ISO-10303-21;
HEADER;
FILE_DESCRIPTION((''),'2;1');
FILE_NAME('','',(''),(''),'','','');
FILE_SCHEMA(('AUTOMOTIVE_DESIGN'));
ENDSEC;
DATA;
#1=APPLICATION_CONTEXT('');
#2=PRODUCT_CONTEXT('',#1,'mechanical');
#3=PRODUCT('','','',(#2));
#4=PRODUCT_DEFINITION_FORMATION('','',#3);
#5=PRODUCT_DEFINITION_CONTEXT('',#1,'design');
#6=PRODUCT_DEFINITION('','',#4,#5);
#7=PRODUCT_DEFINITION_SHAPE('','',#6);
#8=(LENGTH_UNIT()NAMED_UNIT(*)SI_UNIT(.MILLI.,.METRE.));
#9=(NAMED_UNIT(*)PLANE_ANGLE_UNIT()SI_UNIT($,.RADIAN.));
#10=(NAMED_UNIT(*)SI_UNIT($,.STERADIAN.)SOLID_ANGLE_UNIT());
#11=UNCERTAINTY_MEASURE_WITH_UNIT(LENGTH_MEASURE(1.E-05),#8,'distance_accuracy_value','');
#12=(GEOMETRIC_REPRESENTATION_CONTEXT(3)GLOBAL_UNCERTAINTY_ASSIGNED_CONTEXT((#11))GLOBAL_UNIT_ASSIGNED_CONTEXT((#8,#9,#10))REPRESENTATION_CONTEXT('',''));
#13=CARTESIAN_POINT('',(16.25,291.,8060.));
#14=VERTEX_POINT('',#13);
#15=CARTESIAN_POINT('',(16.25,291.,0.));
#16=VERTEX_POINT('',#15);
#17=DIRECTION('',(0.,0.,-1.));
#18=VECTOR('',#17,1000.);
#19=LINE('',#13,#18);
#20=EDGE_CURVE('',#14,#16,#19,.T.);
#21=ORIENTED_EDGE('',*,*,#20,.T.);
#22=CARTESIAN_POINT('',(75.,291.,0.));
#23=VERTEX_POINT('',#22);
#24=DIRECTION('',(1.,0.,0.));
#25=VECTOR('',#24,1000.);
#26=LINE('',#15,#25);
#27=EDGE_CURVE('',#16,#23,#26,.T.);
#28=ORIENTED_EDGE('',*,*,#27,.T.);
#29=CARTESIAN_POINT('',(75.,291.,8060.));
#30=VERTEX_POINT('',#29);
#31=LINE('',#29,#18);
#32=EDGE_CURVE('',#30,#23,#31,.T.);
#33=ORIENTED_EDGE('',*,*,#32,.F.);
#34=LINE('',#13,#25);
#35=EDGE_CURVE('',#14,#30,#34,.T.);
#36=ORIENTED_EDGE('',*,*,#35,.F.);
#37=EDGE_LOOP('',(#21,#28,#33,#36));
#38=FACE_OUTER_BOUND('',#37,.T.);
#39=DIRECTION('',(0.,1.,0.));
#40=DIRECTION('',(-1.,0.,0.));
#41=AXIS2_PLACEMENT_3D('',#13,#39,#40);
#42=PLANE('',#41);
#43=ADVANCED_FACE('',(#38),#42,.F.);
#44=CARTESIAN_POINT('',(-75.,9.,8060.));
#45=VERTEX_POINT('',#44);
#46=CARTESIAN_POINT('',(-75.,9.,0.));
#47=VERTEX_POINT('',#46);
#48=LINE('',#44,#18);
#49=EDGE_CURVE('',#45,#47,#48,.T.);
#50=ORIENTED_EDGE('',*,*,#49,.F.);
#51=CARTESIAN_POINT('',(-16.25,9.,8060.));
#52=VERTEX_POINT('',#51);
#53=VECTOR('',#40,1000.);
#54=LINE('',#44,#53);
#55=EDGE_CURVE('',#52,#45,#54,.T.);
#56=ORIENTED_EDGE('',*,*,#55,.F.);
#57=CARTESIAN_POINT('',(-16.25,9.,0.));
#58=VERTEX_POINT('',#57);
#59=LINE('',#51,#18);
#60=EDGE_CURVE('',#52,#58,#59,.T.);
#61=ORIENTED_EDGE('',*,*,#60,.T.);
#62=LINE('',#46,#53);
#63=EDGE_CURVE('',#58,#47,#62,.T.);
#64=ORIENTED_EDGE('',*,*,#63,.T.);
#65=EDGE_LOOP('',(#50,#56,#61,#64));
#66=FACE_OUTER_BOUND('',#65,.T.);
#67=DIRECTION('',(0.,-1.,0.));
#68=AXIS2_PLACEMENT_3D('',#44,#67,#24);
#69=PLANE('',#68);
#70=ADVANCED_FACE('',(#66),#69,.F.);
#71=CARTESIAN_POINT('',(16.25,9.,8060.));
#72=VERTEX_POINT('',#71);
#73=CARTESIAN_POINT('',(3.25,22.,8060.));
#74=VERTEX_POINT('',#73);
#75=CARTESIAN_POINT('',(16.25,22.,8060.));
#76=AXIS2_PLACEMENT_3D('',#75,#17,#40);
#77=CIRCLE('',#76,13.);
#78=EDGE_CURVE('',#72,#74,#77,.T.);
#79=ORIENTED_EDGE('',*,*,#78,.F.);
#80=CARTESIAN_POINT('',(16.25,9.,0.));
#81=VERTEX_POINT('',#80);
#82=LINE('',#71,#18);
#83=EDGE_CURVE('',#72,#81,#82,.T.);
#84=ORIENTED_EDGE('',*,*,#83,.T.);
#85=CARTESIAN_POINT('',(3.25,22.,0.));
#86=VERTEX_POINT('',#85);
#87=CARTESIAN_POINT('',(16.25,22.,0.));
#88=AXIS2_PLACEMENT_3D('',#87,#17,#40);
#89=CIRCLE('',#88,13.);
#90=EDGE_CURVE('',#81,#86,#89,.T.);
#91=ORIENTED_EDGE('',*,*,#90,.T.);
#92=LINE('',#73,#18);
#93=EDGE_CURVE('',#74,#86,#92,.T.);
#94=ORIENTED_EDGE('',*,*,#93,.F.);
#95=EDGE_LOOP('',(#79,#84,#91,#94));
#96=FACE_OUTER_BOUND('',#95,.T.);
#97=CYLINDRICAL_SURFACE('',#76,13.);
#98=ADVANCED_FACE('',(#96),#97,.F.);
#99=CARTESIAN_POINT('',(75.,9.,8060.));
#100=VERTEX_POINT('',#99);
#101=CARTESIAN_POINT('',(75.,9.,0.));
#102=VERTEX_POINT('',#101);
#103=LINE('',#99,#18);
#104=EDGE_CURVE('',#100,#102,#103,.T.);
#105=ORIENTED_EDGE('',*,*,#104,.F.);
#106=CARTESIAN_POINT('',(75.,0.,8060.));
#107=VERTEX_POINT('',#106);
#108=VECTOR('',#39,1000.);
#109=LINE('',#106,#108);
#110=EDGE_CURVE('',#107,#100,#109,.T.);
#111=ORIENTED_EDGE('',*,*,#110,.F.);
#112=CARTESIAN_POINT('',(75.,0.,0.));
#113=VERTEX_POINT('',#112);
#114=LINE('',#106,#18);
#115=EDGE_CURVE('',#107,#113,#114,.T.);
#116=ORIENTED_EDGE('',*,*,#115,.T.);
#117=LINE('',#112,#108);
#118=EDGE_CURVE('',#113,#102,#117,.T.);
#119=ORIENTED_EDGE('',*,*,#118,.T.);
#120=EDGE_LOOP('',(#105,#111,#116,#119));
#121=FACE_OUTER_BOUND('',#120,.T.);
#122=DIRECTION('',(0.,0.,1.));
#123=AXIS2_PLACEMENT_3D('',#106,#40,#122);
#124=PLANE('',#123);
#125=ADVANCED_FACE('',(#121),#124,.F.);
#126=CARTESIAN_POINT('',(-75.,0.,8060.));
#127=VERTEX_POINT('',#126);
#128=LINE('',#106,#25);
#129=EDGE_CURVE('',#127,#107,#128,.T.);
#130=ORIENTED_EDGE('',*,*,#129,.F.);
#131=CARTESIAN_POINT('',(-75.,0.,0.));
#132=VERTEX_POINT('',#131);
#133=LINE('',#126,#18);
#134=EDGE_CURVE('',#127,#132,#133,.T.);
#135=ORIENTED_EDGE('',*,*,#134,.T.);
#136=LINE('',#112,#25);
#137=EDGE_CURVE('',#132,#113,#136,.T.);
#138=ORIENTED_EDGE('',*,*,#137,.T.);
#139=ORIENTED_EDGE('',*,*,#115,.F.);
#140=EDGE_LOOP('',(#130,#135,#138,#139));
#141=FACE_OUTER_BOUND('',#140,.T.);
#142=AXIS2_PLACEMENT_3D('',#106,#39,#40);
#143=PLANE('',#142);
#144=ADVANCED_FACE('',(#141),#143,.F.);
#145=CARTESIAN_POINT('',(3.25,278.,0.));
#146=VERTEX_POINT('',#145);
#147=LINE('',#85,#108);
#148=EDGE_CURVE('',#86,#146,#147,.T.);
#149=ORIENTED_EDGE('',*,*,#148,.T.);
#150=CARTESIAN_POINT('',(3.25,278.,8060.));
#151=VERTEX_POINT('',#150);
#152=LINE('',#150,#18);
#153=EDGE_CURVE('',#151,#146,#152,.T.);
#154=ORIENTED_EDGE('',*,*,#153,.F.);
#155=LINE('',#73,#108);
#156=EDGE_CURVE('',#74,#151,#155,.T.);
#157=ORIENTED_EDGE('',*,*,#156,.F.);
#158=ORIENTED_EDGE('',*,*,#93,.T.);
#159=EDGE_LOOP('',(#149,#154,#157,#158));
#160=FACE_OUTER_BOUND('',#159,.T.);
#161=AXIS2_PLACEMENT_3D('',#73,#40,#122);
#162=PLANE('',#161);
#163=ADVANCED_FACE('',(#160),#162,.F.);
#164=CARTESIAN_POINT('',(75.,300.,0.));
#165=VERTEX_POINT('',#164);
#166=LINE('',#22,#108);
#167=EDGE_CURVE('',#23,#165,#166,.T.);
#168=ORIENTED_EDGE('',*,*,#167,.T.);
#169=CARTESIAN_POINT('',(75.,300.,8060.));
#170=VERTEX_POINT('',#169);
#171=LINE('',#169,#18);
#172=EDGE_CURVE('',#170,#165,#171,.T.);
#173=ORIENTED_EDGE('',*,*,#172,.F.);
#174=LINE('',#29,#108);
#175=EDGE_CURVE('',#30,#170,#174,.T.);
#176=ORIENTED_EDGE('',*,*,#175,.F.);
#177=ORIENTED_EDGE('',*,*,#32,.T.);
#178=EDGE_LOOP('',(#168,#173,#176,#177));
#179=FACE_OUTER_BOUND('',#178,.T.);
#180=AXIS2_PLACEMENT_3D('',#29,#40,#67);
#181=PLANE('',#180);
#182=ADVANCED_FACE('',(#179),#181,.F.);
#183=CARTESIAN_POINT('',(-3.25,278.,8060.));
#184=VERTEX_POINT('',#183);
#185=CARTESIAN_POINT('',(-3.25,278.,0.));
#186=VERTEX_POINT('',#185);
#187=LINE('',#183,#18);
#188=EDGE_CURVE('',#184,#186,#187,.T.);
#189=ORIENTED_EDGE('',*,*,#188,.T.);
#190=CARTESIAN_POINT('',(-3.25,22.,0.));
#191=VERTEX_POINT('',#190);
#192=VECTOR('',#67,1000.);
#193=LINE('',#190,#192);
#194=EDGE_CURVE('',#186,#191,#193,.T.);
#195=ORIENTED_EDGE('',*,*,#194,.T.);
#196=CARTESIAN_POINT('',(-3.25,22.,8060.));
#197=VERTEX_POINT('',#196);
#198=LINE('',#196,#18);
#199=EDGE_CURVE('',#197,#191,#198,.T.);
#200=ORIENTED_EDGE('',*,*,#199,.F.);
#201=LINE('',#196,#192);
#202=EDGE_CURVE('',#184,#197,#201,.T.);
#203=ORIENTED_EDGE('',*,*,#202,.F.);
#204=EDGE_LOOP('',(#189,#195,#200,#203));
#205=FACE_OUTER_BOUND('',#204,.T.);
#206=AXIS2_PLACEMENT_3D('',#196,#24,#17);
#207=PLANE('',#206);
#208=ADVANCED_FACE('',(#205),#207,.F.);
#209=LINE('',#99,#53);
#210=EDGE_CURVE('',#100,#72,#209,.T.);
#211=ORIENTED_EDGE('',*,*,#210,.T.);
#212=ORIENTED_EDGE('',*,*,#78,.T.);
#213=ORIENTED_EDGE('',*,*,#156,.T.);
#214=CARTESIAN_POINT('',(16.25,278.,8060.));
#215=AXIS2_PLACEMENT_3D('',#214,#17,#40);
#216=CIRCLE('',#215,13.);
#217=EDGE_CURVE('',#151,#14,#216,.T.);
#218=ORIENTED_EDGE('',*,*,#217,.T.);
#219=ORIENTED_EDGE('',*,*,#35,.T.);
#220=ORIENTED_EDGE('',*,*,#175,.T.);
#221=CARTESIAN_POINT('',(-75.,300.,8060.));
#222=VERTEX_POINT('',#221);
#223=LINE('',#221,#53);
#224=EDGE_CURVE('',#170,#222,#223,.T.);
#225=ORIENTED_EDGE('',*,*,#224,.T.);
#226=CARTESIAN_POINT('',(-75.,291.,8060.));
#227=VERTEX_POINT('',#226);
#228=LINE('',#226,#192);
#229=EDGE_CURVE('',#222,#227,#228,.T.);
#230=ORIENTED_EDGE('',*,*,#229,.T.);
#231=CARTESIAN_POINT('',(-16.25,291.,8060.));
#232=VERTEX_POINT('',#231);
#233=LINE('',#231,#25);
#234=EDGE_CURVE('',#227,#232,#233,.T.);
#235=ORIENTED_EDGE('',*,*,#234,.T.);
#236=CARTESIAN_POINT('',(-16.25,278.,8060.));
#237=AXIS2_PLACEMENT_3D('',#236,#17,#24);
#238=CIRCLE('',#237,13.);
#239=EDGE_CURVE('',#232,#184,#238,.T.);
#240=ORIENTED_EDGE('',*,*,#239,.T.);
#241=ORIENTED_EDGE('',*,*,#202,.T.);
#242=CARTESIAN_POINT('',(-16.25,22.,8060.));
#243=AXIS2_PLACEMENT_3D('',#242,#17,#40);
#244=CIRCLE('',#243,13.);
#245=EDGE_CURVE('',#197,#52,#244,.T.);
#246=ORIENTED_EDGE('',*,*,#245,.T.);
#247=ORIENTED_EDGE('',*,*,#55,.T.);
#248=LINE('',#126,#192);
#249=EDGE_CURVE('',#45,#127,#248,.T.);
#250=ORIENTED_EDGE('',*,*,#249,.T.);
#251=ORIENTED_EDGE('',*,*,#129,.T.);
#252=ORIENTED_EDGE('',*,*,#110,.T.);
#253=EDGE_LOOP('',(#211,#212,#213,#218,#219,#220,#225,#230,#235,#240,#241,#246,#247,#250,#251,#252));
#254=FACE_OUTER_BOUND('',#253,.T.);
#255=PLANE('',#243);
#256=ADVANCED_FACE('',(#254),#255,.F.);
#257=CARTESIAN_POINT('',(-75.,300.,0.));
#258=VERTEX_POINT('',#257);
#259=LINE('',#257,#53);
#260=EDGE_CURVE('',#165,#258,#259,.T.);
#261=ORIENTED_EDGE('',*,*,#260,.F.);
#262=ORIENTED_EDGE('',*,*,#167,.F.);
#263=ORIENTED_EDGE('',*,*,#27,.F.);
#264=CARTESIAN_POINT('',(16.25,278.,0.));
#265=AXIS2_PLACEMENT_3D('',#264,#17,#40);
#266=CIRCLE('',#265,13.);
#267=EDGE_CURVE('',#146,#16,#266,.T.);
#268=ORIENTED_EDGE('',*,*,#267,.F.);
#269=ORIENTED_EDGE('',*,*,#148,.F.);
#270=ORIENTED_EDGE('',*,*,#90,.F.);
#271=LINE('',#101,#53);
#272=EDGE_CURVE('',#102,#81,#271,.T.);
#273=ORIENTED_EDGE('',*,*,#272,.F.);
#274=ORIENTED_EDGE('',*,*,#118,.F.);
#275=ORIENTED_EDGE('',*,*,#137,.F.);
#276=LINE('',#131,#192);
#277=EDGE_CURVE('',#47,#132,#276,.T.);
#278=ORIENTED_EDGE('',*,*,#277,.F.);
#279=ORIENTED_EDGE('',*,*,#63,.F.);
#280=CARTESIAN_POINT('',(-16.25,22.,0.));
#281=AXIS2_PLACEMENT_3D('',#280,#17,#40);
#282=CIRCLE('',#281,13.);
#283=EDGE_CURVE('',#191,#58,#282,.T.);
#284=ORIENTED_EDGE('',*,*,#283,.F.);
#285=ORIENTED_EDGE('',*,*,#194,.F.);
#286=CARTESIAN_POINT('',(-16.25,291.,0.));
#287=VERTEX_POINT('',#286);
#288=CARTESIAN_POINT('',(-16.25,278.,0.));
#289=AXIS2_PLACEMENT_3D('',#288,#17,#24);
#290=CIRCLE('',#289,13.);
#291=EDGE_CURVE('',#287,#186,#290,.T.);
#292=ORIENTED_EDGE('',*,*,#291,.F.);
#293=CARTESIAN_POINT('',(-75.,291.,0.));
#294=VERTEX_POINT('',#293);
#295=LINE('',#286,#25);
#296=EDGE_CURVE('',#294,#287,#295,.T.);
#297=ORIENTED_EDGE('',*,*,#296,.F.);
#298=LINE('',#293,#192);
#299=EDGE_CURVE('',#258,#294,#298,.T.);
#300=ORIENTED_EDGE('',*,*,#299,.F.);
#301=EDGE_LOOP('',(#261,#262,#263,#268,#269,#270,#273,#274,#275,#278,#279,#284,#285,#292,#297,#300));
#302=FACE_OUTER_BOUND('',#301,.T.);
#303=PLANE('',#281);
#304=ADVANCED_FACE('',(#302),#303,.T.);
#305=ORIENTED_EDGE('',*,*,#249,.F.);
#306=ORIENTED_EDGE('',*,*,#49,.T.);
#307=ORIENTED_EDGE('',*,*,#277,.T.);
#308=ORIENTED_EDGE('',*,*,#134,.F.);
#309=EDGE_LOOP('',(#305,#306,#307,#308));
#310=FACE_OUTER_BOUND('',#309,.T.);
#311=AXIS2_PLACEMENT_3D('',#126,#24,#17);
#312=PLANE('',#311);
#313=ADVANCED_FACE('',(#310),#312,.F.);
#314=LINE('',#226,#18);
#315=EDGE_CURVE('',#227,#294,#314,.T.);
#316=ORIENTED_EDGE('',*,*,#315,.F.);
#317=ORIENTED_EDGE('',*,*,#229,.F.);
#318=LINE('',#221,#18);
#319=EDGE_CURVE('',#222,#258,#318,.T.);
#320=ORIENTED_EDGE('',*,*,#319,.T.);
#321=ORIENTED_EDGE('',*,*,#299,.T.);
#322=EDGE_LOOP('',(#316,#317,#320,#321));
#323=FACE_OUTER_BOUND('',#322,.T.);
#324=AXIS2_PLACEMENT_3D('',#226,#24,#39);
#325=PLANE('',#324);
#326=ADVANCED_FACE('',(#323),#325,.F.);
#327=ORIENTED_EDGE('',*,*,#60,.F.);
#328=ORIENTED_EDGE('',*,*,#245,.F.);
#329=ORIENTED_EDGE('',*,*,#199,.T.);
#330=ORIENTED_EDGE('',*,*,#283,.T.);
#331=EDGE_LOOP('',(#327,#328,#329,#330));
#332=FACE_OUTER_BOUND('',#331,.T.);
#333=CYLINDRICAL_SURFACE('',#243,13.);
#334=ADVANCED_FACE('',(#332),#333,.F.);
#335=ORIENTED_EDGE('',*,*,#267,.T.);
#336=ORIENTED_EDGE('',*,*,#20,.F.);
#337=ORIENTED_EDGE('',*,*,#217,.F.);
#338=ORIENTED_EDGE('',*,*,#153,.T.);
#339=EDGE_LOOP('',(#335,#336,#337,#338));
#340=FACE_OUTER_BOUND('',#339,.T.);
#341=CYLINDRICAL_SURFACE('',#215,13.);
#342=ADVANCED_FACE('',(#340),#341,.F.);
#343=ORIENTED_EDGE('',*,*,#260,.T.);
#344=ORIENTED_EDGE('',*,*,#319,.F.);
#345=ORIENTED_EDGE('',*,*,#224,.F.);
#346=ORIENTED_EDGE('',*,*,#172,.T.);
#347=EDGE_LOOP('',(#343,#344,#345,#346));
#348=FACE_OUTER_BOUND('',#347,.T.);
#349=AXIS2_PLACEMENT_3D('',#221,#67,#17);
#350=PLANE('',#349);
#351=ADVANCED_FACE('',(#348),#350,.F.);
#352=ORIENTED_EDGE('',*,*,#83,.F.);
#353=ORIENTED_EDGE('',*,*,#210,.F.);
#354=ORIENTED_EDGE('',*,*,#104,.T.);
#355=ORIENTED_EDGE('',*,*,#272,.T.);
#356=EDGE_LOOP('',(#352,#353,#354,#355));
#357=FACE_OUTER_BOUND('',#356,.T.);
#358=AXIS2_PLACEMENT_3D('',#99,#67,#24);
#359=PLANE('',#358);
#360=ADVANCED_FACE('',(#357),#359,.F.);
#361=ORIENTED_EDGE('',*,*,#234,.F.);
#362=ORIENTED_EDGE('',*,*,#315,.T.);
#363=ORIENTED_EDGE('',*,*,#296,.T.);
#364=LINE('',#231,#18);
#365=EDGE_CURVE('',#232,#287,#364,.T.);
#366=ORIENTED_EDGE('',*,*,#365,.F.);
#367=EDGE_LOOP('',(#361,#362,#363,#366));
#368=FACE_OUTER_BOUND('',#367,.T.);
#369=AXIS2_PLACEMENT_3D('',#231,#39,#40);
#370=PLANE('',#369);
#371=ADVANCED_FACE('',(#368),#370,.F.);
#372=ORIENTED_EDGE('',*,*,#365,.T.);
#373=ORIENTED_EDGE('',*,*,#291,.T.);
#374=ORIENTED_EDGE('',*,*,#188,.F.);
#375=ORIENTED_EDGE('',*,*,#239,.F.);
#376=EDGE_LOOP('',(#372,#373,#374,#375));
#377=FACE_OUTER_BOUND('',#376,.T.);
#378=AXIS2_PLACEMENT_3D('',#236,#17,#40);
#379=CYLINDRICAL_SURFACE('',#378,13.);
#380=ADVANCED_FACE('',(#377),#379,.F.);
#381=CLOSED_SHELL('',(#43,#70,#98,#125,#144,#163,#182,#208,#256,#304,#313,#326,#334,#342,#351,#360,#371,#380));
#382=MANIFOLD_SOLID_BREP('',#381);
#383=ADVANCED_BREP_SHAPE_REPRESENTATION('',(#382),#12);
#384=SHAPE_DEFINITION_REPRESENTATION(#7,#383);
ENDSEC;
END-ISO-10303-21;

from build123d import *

# Parameters (mm, degrees)
BOSS_EXTRUDE1_DEPTH = 8060


with BuildPart() as part:
    # Sketch1 → Boss-Extrude1 (new body)
    with BuildSketch(Plane.XY):
        with BuildLine():
            Line((75, 0), (-75, 0))
            Line((-75, 0), (-75, 9))
            Line((-75, 9), (-16.25, 9))
            ThreePointArc((-16.25, 9), (-7.057611845, 12.807611845), (-3.25, 22))
            Line((-3.25, 22), (-3.25, 278))
            ThreePointArc((-3.25, 278), (-7.057611845, 287.192388155), (-16.25, 291))
            Line((-16.25, 291), (-75, 291))
            Line((-75, 291), (-75, 300))
            Line((-75, 300), (75, 300))
            Line((75, 300), (75, 291))
            Line((75, 291), (16.25, 291))
            ThreePointArc((16.25, 291), (7.057611845, 287.192388155), (3.25, 278))
            Line((3.25, 278), (3.25, 22))
            ThreePointArc((3.25, 22), (7.057611845, 12.807611845), (16.25, 9))
            Line((16.25, 9), (75, 9))
            Line((75, 9), (75, 0))
        make_face()
    extrude(amount=BOSS_EXTRUDE1_DEPTH)


solid = part.part
